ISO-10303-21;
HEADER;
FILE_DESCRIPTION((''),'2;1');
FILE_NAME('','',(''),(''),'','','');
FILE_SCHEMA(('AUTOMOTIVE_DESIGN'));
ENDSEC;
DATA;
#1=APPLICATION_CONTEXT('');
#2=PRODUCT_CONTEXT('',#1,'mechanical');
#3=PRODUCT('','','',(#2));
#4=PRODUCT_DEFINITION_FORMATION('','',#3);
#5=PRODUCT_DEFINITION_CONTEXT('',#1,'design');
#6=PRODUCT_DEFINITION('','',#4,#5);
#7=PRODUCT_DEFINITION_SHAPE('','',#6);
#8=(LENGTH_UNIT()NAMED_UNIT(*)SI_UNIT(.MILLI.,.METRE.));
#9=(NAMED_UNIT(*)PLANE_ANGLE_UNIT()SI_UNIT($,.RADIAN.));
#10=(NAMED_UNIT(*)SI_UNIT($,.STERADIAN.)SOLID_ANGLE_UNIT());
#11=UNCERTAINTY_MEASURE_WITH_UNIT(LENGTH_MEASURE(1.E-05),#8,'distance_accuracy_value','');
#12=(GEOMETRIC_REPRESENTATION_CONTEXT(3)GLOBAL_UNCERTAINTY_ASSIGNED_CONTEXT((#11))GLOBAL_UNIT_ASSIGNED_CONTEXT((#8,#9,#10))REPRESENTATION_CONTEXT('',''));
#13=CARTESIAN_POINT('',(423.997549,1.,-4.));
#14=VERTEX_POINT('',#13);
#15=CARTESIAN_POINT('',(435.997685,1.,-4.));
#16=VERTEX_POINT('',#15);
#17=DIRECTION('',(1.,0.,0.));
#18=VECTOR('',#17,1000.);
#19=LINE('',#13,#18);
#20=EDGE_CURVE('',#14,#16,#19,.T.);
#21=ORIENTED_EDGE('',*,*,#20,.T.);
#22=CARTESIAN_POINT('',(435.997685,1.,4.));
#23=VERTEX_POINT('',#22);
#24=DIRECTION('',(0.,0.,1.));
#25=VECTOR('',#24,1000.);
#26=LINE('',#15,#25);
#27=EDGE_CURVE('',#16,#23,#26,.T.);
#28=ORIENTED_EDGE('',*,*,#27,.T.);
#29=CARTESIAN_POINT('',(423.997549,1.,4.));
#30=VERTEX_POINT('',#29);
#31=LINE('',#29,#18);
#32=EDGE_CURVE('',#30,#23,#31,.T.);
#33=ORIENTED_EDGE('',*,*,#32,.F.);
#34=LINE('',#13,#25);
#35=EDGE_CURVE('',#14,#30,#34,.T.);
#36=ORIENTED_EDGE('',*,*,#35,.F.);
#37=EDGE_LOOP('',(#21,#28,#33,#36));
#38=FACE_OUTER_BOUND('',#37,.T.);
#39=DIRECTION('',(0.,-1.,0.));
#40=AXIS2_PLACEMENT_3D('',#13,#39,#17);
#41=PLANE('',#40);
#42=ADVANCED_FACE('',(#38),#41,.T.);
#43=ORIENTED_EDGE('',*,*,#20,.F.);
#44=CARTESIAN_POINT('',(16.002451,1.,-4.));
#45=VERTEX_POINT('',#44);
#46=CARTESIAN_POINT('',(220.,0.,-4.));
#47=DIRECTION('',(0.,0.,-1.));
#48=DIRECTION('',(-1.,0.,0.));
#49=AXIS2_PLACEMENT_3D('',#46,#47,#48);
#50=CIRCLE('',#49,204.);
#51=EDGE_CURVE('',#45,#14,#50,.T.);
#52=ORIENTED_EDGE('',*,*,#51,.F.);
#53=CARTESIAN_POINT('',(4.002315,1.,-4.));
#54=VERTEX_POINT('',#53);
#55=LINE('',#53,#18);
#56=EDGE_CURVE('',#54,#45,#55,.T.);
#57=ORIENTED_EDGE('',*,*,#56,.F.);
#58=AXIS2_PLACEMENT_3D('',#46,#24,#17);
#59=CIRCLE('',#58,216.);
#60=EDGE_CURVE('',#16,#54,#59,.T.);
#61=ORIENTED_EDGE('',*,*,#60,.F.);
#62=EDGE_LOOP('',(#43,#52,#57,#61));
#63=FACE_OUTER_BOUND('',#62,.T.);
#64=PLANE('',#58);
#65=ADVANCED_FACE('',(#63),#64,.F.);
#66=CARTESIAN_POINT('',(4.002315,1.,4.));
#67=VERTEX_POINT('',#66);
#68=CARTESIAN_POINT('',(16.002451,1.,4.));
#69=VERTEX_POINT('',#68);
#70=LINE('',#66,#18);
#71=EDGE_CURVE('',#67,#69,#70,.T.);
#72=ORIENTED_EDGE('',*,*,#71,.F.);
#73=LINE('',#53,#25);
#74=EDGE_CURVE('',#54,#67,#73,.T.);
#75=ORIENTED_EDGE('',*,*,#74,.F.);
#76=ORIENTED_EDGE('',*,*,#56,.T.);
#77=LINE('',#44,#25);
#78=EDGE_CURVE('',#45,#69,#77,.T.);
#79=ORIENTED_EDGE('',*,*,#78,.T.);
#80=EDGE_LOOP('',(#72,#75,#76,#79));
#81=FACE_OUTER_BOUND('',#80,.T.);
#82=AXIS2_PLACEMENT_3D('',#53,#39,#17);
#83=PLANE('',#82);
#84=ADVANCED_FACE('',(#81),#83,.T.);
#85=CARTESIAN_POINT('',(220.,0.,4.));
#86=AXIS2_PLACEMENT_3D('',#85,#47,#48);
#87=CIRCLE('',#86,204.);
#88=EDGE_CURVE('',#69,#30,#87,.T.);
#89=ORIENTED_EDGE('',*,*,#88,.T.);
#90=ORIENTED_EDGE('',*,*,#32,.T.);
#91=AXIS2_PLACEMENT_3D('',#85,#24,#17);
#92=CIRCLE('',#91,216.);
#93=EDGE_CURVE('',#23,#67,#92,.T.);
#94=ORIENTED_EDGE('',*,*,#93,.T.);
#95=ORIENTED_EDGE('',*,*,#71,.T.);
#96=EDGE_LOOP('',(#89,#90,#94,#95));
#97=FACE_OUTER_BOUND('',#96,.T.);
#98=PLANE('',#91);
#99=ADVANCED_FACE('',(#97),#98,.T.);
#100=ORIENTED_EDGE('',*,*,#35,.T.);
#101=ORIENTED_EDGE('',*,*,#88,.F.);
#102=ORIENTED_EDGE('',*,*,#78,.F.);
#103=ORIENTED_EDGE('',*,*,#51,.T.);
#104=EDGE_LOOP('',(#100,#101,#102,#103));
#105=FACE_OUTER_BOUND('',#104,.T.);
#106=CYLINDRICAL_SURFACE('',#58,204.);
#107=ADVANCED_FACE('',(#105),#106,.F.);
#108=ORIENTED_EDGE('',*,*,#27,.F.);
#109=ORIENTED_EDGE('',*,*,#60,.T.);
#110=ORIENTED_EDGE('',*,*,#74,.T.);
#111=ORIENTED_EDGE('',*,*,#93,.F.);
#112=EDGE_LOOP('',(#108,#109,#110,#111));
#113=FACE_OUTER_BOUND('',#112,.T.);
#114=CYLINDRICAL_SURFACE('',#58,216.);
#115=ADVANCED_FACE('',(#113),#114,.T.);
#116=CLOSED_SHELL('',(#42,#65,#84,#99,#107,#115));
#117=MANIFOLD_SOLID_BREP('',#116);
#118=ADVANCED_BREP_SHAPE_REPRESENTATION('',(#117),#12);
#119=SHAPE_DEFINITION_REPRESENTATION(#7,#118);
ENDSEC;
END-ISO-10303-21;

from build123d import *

# Parameters (mm, degrees)
EXTRUDE_1_DEPTH = 4


with BuildPart() as part:
    # 草图1 → 凸台-拉伸1 (new, symmetric)
    with BuildSketch(Plane.XY):
        with BuildLine():
            Line((4.002314827, 1), (16.002450995, 1))
            ThreePointArc((16.002450995, 1), (220, 204), (423.997549005, 1))
            Line((423.997549005, 1), (435.997685173, 1))
            ThreePointArc((435.997685173, 1), (220, 216), (4.002314827, 1))
        make_face()
    extrude(amount=EXTRUDE_1_DEPTH, both=True)


solid = part.part
